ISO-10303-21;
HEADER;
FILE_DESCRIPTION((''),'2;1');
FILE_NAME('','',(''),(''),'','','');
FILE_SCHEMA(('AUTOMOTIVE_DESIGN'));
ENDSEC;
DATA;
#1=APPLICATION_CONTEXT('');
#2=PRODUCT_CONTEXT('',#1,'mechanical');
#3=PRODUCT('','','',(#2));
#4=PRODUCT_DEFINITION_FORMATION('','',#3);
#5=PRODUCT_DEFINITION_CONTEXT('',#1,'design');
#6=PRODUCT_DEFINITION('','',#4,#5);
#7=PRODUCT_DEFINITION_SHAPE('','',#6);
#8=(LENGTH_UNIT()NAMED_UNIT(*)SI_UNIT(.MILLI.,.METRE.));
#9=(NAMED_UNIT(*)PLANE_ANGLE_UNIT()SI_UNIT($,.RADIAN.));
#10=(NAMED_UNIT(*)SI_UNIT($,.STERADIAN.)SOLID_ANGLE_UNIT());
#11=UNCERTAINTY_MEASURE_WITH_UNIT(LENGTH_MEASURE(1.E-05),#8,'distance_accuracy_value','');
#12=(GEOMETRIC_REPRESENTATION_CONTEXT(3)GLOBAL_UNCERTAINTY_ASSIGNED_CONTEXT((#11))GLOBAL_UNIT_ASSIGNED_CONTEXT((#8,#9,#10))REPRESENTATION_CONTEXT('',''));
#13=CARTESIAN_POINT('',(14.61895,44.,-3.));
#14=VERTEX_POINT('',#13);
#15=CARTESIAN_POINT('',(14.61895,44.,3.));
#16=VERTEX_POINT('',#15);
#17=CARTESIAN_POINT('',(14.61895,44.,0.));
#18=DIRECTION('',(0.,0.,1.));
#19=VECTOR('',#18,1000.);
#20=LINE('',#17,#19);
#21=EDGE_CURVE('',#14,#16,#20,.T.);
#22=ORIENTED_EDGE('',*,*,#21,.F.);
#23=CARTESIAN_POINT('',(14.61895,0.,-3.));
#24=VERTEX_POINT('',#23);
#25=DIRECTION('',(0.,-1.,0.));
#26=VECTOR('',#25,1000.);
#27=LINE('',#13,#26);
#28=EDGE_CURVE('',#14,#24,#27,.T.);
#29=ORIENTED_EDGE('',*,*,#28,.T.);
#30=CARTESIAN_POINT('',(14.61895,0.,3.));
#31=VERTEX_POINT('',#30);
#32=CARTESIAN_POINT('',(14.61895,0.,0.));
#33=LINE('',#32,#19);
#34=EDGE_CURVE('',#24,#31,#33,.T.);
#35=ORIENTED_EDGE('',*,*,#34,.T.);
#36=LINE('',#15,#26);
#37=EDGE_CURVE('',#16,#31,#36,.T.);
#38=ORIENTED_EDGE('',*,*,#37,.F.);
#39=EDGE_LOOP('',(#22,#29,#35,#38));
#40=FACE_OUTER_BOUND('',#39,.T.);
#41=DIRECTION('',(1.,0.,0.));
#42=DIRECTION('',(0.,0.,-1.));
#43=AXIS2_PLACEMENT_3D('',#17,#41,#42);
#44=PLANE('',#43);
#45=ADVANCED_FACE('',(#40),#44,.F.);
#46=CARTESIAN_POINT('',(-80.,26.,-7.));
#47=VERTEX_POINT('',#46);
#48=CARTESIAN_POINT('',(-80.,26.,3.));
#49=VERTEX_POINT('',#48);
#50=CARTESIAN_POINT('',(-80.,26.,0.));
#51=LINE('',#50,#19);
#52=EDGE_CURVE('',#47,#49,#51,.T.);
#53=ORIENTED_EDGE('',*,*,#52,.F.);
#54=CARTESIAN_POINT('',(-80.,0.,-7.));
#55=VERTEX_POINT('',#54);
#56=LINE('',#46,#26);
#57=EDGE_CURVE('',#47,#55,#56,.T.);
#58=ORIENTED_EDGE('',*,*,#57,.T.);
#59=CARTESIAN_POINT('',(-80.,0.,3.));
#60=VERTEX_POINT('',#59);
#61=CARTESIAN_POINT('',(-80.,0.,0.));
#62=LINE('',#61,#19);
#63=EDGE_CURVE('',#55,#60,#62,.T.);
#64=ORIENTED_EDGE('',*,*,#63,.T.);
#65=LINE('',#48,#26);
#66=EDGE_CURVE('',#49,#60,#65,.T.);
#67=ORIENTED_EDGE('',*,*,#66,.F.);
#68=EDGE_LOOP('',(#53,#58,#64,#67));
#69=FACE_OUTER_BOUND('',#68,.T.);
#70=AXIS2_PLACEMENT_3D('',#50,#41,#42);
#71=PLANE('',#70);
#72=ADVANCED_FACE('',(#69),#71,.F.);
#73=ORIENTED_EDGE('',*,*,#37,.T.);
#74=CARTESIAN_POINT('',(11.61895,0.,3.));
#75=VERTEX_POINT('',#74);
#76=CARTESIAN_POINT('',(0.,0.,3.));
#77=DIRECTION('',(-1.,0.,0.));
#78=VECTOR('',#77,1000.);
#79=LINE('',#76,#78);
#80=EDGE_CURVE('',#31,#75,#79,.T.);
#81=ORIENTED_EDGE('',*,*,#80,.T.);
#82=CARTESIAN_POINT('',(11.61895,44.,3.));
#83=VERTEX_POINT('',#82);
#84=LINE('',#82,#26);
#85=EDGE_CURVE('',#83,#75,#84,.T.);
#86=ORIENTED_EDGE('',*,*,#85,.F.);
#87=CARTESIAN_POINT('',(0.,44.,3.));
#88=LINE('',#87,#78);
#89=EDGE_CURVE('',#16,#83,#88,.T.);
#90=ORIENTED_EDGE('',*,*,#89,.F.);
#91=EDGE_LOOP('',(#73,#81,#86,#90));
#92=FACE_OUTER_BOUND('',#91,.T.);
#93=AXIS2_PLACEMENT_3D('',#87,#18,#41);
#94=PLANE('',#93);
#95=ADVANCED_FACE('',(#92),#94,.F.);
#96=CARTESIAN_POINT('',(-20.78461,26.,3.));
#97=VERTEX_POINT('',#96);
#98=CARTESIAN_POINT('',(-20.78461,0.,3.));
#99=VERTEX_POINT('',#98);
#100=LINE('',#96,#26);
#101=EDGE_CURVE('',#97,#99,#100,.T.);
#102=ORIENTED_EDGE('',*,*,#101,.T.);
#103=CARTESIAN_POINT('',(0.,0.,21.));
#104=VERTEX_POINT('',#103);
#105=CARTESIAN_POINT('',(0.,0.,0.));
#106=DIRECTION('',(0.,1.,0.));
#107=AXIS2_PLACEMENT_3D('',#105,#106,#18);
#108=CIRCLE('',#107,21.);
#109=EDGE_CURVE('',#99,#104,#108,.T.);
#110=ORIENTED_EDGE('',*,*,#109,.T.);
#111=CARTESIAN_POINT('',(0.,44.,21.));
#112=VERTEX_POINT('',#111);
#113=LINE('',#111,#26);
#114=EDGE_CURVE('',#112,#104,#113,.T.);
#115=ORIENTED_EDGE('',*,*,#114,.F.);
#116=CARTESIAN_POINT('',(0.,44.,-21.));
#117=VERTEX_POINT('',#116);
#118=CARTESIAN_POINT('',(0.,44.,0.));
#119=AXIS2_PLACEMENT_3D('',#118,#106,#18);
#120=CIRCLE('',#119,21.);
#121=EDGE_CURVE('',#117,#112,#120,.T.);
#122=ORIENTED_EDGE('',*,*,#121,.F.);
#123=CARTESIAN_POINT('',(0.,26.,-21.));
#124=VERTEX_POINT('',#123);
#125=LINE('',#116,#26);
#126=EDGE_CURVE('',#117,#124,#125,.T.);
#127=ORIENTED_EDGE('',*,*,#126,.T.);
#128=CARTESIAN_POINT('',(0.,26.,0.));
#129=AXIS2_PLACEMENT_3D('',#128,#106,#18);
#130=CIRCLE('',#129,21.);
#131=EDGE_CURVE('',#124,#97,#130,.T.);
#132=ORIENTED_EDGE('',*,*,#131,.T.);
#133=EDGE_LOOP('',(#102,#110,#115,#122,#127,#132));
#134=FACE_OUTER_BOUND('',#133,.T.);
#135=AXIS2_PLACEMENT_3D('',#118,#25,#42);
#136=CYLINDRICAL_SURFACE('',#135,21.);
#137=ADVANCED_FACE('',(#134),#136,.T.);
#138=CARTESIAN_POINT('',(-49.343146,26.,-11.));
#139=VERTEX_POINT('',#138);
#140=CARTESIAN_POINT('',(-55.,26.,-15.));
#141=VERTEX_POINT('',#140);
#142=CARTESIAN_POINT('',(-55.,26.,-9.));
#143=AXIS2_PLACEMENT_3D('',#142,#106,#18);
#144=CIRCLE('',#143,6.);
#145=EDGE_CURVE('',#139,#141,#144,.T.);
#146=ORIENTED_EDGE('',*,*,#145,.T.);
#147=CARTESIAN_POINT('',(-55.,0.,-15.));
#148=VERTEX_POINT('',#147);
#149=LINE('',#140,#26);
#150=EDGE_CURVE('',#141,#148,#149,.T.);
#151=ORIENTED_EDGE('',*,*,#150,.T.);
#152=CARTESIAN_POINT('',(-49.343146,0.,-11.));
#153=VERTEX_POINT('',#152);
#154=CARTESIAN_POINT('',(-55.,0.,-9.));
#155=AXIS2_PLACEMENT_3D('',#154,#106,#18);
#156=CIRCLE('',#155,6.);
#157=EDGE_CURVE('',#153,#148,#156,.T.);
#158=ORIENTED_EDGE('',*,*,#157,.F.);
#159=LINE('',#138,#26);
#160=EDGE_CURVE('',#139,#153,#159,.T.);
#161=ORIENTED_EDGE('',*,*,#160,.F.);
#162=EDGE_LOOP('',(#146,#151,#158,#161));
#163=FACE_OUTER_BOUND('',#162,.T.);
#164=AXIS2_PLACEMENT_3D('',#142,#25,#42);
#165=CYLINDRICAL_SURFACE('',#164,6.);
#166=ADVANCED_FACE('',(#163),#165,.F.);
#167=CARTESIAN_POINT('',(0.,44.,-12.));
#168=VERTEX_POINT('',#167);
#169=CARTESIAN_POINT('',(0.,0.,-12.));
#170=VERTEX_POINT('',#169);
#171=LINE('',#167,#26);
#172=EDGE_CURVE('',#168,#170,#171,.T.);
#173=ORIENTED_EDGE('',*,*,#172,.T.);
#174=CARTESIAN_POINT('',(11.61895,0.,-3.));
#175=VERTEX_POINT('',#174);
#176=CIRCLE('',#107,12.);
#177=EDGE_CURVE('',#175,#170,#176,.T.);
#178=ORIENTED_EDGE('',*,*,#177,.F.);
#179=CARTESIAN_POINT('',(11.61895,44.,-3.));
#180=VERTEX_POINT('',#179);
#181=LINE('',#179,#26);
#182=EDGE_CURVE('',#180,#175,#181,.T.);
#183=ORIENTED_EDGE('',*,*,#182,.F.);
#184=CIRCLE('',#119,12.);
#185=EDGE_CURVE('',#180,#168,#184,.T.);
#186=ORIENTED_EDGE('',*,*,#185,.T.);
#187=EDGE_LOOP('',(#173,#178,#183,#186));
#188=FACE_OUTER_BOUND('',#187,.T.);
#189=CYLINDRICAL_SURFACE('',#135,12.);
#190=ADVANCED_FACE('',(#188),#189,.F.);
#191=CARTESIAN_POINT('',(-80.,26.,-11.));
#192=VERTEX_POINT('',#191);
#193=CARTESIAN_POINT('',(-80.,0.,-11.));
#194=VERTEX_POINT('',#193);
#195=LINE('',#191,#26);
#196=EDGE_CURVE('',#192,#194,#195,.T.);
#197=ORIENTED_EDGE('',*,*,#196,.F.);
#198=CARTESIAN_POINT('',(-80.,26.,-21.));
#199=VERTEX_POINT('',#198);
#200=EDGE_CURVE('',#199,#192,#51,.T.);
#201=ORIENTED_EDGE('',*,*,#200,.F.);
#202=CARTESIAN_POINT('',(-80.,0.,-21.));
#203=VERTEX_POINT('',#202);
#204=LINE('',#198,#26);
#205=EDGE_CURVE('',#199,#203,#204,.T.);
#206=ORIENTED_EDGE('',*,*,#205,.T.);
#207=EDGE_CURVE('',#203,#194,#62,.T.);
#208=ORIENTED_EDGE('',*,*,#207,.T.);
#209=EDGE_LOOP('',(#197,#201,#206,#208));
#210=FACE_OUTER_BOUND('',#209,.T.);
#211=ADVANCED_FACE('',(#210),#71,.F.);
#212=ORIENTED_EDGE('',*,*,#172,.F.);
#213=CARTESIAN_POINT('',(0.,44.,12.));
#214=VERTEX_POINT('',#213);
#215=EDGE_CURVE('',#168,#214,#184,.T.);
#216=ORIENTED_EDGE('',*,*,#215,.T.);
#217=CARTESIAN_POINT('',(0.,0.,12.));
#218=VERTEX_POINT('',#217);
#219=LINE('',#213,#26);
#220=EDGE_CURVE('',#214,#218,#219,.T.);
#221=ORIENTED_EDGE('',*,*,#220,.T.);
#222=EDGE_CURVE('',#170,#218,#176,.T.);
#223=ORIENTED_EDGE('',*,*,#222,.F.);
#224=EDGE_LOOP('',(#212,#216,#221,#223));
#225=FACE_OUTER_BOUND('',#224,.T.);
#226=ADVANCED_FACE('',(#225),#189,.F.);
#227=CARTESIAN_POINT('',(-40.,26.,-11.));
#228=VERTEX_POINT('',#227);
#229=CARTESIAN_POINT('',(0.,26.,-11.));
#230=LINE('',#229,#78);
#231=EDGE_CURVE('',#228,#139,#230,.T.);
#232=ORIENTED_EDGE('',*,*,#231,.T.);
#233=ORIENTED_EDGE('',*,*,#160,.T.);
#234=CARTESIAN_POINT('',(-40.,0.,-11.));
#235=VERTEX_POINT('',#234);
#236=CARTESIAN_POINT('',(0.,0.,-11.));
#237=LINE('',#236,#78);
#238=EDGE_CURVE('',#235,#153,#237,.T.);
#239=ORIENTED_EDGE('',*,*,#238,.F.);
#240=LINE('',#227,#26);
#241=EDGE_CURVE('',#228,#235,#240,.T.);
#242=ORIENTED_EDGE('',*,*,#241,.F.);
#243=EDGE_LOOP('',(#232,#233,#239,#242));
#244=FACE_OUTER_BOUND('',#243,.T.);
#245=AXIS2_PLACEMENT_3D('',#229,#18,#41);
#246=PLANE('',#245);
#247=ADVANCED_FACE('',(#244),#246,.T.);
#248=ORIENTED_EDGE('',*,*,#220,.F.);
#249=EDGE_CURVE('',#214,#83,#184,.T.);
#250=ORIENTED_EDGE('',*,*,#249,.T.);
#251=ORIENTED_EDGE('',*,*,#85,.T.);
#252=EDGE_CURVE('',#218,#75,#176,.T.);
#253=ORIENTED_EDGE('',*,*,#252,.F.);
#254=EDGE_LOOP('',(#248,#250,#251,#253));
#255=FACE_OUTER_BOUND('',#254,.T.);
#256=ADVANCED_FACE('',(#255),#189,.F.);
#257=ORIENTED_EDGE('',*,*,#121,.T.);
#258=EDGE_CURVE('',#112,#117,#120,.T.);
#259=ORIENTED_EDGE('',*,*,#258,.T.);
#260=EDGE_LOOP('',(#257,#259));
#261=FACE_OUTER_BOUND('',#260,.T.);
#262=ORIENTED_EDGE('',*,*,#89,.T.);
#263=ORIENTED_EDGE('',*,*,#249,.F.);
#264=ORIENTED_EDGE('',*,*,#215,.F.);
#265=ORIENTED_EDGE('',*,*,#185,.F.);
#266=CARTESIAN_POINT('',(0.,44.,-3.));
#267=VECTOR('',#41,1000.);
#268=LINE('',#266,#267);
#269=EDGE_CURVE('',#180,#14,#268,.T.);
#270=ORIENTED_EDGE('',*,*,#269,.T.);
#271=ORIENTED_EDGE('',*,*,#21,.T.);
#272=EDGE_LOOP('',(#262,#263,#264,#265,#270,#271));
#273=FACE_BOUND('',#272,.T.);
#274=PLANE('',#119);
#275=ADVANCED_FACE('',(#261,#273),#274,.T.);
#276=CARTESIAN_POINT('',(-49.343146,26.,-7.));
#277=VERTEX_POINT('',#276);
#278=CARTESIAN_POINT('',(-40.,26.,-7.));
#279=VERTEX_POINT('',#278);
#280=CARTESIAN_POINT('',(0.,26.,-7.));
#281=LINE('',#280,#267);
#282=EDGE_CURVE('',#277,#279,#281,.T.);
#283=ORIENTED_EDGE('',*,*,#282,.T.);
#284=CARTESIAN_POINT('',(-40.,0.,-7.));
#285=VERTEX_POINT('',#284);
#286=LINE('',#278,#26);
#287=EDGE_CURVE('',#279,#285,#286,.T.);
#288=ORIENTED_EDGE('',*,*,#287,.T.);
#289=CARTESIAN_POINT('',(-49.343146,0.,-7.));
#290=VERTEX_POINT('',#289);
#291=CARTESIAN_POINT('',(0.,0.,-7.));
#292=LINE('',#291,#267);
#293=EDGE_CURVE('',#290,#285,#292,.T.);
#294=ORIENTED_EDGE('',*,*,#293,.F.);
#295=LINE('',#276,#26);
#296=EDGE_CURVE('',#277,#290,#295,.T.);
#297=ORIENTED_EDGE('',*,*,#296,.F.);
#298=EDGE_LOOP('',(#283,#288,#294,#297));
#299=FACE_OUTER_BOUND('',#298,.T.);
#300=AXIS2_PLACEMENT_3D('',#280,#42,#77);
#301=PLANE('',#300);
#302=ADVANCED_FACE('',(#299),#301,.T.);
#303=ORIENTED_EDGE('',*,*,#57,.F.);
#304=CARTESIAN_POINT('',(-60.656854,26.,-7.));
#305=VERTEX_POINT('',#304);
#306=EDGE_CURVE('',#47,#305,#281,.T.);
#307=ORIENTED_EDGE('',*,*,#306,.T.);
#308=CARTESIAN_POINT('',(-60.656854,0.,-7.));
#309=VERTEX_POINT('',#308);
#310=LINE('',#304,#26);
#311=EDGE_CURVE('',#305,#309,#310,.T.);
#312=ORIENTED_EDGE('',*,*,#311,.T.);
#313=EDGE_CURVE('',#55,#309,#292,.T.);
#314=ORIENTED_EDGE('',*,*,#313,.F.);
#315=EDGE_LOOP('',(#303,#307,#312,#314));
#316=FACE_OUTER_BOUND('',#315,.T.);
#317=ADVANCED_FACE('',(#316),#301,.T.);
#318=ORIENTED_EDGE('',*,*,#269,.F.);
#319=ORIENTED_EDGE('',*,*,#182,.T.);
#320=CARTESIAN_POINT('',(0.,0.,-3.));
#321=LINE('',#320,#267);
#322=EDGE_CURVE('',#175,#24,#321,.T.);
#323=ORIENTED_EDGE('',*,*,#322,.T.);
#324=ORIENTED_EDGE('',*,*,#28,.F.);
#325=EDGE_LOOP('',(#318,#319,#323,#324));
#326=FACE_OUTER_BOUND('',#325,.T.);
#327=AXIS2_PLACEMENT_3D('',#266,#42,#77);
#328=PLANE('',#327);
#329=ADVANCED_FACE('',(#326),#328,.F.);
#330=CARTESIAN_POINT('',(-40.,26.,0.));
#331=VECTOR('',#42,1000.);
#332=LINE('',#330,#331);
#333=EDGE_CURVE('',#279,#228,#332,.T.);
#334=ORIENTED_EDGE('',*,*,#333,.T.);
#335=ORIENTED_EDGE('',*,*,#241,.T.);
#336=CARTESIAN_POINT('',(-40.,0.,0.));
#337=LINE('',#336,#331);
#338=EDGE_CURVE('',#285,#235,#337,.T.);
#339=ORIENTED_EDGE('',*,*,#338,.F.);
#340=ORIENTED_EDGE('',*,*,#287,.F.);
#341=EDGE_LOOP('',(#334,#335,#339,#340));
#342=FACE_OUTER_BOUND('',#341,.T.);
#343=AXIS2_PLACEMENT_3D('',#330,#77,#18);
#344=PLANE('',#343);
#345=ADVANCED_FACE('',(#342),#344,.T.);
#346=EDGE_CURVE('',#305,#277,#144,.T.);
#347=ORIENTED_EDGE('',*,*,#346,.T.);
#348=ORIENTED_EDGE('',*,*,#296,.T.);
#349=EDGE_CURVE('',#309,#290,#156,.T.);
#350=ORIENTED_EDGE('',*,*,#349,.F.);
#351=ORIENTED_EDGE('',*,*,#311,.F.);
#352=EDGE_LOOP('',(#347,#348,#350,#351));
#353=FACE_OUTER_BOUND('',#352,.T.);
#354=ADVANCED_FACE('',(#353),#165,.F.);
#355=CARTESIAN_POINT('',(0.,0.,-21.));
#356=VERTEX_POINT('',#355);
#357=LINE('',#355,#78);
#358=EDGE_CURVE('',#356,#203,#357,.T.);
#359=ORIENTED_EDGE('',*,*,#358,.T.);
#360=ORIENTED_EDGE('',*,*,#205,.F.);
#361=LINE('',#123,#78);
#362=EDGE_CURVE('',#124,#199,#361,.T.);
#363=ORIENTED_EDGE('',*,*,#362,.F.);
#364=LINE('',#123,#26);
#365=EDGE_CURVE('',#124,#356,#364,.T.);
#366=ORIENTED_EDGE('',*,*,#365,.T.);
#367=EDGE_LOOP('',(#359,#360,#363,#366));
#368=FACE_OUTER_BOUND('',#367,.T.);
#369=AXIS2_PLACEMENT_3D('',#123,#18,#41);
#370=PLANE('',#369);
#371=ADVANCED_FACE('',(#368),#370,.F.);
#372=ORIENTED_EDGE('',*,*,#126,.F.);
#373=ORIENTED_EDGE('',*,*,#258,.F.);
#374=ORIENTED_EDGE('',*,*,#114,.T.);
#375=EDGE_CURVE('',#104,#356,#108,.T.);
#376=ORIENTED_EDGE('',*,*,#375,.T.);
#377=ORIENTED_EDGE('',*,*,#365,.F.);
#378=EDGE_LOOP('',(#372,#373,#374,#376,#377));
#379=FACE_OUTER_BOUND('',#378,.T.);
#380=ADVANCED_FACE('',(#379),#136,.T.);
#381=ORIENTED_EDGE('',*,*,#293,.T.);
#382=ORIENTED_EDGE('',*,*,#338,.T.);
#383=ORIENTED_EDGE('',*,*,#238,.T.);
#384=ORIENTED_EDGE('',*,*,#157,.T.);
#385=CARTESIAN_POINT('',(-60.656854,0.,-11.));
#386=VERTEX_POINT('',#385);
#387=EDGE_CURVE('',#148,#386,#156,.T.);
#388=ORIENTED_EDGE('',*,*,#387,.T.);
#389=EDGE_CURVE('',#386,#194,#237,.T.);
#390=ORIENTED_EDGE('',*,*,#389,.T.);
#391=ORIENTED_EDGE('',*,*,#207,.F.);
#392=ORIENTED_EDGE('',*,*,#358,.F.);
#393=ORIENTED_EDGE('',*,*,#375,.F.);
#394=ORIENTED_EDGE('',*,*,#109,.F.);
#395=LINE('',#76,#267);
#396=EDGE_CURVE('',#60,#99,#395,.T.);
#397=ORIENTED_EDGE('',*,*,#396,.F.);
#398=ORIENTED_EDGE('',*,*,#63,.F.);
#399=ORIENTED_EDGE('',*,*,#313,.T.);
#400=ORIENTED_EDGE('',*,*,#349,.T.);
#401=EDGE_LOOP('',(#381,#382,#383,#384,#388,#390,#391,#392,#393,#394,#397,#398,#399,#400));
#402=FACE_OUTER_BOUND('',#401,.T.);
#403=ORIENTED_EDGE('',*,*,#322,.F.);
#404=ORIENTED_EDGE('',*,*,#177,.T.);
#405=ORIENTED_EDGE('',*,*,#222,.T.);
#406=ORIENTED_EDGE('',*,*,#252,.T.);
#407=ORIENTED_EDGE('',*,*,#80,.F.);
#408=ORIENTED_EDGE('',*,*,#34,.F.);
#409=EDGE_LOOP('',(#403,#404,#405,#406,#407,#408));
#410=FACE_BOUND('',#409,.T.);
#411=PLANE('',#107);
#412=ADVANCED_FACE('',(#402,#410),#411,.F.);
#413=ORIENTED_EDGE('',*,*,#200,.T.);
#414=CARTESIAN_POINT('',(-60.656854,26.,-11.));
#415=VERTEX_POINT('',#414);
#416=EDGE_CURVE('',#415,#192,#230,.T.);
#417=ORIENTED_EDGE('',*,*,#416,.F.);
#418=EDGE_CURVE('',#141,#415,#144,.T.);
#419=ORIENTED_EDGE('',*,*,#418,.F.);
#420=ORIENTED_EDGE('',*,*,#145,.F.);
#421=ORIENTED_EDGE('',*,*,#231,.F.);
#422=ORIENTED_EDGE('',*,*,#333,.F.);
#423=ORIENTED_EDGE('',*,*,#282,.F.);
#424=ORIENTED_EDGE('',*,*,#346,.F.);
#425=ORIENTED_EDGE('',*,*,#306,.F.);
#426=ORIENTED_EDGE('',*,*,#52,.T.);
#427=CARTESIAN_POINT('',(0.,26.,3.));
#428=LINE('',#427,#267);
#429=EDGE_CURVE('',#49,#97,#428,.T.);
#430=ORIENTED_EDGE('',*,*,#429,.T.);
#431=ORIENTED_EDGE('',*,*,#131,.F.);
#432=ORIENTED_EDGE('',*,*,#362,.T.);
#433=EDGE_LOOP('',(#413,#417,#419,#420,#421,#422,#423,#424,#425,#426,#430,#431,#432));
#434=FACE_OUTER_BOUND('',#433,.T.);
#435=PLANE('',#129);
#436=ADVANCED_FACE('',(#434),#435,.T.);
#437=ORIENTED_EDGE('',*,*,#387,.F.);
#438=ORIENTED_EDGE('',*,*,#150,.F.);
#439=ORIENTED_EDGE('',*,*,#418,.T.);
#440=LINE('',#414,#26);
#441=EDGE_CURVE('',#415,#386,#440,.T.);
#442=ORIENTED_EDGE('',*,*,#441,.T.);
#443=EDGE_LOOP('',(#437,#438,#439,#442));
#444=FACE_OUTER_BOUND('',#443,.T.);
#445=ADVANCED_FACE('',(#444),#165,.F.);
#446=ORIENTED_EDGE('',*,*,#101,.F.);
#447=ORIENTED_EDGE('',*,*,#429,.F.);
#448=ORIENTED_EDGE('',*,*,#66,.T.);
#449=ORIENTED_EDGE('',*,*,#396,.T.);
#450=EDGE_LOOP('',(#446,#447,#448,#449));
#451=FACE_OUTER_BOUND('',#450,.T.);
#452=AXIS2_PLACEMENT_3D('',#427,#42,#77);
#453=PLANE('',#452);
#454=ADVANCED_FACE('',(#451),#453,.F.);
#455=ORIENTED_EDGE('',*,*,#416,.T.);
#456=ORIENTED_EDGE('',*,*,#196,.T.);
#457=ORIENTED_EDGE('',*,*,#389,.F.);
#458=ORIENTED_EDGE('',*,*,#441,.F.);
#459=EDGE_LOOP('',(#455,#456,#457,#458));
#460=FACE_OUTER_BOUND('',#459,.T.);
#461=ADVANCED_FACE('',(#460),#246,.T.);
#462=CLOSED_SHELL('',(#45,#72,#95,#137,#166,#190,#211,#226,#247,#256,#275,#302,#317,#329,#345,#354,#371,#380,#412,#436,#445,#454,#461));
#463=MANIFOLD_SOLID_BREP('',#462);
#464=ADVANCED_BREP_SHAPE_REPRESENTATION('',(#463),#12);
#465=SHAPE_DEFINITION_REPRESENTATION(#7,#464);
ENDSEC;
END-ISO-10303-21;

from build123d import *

# Parameters (mm, degrees)
LEVER_PROFILE_SKETCH_R      = 21
HUB_BOSS_44MM_DEPTH         = 44
SLOTTED_ARM_BOSS_26MM_DEPTH = 26


with BuildPart() as part:
    # Lever Profile Sketch → Hub Boss 44mm (new body)
    with BuildSketch(Plane(origin=(0, 0, 0), x_dir=(1, 0, 0), z_dir=(0, 1, 0))):
        with Locations(Location((0, 0, 0), (0, 0, 270))):
            Circle(LEVER_PROFILE_SKETCH_R)
        with BuildLine():
            Line((11.618950039, 3), (14.618950039, 3))
            Line((14.618950039, 3), (14.618950039, -3))
            Line((14.618950039, -3), (11.618950039, -3))
            ThreePointArc((11.618950039, -3), (-12, 0), (11.618950039, 3))
        make_face(mode=Mode.SUBTRACT)
    extrude(amount=HUB_BOSS_44MM_DEPTH)

    # Sketch1_3 → Slotted Arm Boss 26mm (add)
    with BuildSketch(Plane(origin=(0, 0, 0), x_dir=(1, 0, 0), z_dir=(0, 1, 0))):
        with BuildLine():
            ThreePointArc((-20.784609691, -3), (-15.874507866, 13.747727085), (0, 21))
            Line((0, 21), (-80, 21))
            Line((-80, 21), (-80, 11))
            Line((-80, 11), (-60.656854249, 11))
            ThreePointArc((-60.656854249, 11), (-55, 15), (-49.343145751, 11))
            Line((-49.343145751, 11), (-40, 11))
            Line((-40, 11), (-40, 7))
            Line((-40, 7), (-49.343145751, 7))
            ThreePointArc((-49.343145751, 7), (-55, 3), (-60.656854249, 7))
            Line((-60.656854249, 7), (-80, 7))
            Line((-80, 7), (-80, -3))
            Line((-80, -3), (-20.784609691, -3))
        make_face()
    extrude(amount=SLOTTED_ARM_BOSS_26MM_DEPTH)


solid = part.part
